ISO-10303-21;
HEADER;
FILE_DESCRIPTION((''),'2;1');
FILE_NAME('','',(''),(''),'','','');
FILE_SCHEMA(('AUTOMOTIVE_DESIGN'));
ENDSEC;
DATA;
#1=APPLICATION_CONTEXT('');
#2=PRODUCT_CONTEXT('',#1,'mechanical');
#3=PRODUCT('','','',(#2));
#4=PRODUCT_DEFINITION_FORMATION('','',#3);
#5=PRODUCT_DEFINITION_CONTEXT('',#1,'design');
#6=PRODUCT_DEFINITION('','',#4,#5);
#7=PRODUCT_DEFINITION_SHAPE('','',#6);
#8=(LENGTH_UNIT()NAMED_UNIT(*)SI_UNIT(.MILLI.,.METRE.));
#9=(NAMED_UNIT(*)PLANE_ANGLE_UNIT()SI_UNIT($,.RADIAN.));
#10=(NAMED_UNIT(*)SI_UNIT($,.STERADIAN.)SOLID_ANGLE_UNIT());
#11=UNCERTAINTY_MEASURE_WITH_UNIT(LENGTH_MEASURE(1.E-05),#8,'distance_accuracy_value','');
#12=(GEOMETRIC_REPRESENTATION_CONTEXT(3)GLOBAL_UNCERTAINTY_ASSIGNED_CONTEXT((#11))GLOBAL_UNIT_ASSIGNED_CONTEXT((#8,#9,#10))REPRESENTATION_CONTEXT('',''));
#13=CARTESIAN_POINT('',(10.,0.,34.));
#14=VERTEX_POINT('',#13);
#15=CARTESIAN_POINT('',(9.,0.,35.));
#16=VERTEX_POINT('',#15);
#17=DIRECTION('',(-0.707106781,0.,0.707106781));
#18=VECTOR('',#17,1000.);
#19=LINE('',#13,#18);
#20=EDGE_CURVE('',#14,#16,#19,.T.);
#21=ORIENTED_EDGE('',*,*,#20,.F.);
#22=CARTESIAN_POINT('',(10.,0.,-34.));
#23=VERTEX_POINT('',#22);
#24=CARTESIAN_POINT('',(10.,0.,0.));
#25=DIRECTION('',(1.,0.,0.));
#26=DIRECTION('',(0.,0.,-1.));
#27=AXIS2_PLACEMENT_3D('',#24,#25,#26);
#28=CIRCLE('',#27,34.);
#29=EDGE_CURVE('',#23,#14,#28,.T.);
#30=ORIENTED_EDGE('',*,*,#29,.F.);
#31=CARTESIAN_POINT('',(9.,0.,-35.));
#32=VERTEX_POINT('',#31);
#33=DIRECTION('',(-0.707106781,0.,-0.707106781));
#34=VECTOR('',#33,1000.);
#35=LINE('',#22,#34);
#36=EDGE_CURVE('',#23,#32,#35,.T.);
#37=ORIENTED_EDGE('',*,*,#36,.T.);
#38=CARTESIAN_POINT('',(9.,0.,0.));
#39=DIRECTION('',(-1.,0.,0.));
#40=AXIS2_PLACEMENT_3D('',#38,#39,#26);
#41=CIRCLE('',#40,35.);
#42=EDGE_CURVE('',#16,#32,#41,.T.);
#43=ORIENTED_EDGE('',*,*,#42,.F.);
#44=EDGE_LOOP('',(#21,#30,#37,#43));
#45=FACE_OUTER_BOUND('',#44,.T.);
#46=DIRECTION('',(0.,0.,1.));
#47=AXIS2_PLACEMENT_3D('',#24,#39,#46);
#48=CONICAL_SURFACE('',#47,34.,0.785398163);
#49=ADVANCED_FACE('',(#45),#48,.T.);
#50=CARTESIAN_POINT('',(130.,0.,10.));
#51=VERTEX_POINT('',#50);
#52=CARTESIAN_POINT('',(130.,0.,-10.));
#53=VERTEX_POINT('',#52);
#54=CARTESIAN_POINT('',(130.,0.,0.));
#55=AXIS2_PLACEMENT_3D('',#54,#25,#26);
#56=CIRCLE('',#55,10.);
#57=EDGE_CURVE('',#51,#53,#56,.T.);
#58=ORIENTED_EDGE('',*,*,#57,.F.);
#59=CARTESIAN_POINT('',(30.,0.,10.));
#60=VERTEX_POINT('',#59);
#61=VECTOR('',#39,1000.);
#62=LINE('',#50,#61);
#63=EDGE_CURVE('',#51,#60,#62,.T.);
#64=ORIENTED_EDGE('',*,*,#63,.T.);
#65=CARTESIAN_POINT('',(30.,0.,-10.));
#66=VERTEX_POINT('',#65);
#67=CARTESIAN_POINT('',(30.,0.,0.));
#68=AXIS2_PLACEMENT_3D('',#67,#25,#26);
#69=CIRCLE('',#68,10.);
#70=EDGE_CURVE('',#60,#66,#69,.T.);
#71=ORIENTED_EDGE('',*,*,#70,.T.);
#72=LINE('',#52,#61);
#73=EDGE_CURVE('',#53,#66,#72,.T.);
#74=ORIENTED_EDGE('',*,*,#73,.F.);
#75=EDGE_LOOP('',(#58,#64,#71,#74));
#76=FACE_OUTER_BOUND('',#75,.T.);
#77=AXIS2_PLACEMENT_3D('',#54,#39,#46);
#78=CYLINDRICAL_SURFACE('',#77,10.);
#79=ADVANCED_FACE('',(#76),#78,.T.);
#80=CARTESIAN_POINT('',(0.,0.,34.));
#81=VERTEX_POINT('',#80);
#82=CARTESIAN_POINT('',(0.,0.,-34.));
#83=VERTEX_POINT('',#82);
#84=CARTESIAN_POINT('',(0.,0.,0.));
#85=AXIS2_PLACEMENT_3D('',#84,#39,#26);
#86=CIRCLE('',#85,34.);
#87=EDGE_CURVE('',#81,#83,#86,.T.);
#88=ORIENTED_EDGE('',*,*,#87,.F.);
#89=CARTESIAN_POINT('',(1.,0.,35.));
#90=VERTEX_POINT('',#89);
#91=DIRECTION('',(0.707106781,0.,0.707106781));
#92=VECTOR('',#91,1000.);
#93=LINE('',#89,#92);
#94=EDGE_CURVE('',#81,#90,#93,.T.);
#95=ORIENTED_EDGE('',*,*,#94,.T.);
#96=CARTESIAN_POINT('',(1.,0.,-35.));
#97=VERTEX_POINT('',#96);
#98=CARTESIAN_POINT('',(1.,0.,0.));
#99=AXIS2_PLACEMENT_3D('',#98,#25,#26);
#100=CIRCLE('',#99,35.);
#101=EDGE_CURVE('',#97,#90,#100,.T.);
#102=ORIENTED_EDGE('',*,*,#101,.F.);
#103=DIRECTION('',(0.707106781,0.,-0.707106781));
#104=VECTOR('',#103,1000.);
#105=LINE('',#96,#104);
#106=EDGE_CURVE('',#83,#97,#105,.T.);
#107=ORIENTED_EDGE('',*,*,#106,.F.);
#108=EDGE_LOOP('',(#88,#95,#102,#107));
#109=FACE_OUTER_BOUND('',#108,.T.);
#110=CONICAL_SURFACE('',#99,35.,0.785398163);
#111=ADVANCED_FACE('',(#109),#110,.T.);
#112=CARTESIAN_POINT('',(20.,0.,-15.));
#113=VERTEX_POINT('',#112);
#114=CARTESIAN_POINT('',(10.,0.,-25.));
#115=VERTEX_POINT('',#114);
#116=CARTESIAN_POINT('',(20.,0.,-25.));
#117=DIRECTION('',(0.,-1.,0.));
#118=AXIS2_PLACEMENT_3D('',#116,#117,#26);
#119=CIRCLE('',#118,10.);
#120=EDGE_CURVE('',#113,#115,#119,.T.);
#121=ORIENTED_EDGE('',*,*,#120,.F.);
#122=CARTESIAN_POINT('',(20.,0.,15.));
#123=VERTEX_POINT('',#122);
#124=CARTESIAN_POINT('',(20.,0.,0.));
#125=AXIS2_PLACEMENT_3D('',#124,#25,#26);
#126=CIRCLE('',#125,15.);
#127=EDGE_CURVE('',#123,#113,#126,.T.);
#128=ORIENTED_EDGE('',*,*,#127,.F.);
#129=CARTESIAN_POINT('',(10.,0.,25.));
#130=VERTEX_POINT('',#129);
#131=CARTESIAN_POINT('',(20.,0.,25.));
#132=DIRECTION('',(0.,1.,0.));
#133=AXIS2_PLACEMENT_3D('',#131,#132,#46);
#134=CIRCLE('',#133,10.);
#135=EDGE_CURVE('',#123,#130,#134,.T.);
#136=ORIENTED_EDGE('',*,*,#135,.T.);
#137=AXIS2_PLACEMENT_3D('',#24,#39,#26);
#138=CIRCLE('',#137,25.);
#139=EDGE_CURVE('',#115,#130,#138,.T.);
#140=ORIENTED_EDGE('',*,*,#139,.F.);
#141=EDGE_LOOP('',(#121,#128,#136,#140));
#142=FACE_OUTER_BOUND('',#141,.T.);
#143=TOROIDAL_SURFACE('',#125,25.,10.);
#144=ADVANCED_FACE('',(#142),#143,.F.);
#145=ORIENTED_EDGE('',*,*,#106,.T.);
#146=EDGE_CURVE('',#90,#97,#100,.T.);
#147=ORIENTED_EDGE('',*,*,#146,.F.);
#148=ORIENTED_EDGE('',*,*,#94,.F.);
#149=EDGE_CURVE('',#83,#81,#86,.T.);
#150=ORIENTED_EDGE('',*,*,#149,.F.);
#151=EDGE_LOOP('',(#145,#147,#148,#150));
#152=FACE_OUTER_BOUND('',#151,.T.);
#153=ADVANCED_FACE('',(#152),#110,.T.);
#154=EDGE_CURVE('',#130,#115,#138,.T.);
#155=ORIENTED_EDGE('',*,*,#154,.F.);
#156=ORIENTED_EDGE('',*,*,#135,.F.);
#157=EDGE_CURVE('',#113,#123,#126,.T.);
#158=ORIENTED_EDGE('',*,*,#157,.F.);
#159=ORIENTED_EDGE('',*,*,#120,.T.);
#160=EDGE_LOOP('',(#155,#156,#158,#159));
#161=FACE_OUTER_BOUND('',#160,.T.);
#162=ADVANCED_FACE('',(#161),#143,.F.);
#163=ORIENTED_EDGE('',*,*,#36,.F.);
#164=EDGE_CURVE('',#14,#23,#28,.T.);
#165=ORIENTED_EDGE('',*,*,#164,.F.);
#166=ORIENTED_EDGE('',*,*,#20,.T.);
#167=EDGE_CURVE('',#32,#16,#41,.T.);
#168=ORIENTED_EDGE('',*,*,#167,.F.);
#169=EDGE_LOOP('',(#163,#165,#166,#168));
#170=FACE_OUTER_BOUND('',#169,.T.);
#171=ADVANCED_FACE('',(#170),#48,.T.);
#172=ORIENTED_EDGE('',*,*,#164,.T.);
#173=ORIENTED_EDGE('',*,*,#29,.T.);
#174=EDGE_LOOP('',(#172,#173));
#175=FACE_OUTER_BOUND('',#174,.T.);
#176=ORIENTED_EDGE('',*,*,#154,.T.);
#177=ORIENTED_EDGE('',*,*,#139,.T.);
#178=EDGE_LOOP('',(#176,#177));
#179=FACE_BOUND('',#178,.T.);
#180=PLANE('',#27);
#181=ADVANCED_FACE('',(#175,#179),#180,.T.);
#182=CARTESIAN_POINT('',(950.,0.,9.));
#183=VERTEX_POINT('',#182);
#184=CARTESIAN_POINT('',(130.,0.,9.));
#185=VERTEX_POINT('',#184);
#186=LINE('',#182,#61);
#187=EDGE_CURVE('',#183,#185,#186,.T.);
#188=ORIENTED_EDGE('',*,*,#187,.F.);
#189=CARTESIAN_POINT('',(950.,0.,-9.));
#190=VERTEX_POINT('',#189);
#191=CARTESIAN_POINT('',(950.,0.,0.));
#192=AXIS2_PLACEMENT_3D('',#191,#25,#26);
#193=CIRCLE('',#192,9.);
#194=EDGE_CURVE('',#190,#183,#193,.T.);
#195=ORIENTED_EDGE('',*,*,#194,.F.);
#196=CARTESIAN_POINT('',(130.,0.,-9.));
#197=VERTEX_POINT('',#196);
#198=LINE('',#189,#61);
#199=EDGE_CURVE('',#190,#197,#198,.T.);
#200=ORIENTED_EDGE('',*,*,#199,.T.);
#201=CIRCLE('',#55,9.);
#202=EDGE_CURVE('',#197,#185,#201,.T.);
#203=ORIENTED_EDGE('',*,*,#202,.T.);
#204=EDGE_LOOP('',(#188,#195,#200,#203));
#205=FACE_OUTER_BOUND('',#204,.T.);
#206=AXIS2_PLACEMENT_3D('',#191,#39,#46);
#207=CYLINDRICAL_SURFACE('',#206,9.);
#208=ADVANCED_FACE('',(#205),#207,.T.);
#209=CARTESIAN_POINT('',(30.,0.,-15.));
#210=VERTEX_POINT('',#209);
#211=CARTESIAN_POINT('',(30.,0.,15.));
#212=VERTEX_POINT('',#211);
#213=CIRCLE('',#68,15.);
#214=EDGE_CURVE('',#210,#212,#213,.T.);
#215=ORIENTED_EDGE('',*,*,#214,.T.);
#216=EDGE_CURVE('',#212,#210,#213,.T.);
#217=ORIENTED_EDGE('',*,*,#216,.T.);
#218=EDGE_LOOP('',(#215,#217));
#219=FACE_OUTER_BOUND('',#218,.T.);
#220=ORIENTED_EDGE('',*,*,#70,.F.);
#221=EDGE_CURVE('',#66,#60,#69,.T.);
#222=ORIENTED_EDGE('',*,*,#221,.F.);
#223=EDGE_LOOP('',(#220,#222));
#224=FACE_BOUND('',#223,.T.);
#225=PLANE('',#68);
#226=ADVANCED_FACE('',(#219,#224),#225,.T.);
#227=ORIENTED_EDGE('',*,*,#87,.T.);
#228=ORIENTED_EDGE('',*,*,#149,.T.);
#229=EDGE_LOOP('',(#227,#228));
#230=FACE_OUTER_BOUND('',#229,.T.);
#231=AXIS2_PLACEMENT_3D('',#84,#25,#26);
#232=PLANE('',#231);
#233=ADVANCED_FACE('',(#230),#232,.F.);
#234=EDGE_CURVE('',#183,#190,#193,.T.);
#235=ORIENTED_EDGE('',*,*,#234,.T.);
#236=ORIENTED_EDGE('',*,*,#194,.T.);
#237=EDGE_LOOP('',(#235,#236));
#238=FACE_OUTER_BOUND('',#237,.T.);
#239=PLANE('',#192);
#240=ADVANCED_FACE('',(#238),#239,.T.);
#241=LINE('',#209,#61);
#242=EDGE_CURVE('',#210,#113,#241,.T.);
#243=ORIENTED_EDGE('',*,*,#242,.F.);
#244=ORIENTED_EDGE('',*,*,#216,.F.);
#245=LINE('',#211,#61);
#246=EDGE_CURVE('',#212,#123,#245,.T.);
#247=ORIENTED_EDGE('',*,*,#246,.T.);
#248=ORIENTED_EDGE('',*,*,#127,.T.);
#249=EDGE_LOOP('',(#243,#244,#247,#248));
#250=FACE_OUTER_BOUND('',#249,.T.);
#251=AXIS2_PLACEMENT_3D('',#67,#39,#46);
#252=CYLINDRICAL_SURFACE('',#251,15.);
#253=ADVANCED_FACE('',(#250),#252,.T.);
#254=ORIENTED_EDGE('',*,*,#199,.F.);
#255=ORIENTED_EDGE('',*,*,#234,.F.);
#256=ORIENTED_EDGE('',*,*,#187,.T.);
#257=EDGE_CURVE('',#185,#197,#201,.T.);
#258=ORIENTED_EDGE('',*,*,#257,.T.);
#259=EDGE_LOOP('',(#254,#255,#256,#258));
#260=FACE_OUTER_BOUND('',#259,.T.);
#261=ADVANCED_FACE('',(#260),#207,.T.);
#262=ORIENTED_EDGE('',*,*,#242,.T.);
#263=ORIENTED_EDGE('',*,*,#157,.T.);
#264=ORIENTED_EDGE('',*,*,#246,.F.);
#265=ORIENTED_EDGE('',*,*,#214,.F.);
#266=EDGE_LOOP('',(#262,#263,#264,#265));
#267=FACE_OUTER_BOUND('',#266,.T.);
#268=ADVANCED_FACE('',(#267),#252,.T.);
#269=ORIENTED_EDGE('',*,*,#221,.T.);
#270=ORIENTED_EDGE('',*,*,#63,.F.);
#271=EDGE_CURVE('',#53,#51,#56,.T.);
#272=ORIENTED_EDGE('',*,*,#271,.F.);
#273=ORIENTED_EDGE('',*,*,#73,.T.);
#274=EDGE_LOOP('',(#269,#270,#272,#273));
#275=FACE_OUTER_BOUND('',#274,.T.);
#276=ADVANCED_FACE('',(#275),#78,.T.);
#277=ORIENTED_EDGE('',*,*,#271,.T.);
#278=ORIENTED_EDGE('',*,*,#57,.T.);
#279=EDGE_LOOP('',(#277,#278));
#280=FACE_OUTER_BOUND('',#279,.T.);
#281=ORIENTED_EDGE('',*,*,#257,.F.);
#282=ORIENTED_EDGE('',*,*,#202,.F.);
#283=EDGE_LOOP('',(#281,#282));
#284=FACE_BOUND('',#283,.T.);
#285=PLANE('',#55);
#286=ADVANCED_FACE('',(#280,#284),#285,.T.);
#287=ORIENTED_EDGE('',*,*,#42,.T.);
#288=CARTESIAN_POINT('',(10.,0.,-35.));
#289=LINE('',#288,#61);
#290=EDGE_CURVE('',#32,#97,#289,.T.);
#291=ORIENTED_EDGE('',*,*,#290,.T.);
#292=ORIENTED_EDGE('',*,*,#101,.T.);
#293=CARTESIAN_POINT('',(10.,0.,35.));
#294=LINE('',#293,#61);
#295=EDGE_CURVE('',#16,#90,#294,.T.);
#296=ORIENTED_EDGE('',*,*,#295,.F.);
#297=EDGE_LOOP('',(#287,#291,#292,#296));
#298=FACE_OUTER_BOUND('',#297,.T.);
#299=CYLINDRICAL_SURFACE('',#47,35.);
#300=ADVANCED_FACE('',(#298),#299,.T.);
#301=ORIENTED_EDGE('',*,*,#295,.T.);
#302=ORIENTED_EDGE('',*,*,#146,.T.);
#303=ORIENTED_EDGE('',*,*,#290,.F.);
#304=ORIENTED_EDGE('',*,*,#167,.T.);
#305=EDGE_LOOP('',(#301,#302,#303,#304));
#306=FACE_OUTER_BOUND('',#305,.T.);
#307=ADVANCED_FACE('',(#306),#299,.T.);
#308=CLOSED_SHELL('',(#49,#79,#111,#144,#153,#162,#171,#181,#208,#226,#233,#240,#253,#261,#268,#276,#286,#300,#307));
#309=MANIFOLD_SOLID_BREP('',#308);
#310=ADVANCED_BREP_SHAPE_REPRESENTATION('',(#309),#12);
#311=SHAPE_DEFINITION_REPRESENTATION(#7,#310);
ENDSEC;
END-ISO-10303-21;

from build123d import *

# Parameters (mm, degrees)
SKETCH_1_R      = 35
EXTRUDE_1_DEPTH = 10
SKETCH_2_R      = 15
EXTRUDE_2_DEPTH = 20
SKETCH_3_R      = 10
EXTRUDE_3_DEPTH = 100
SKETCH_4_R      = 9
EXTRUDE_4_DEPTH = 820
CHAMFER_1_SIZE  = 1
FILLET_1_R      = 10


with BuildPart() as part:
    # 草图1 → 凸台-拉伸1 (new body)
    with BuildSketch(Plane(origin=(0, 0, 0), x_dir=(0, 0, -1), z_dir=(1, 0, 0))):
        Circle(SKETCH_1_R)
    extrude(amount=EXTRUDE_1_DEPTH)

    # 草图2 → 凸台-拉伸2 (add)
    with BuildSketch(Plane(origin=(10, 0, 0), x_dir=(0, 0, -1), z_dir=(1, 0, 0))):
        Circle(SKETCH_2_R)
    extrude(amount=EXTRUDE_2_DEPTH)

    # 草图3 → 凸台-拉伸3 (add)
    with BuildSketch(Plane(origin=(30, 0, 0), x_dir=(0, 0, -1), z_dir=(1, 0, 0))):
        Circle(SKETCH_3_R)
    extrude(amount=EXTRUDE_3_DEPTH)

    # 草图4 → 凸台-拉伸4 (add)
    with BuildSketch(Plane(origin=(130, 0, 0), x_dir=(0, 0, -1), z_dir=(1, 0, 0))):
        with Locations(Location((0, 0, 0), (0, 0, 180))):
            Circle(SKETCH_4_R)
    extrude(amount=EXTRUDE_4_DEPTH)

    # 倒角1
    chamfer_1_edges = [part.edges().sort_by_distance(p)[0] for p in [
        (0, 0, 35),
        (10, 0, 35),
    ]]
    chamfer(chamfer_1_edges, length=CHAMFER_1_SIZE)

    # 圆角1
    fillet_1_edges = [part.edges().sort_by_distance(p)[0] for p in [
        (10, 0, 15),
    ]]
    fillet(fillet_1_edges, radius=FILLET_1_R)


solid = part.part
